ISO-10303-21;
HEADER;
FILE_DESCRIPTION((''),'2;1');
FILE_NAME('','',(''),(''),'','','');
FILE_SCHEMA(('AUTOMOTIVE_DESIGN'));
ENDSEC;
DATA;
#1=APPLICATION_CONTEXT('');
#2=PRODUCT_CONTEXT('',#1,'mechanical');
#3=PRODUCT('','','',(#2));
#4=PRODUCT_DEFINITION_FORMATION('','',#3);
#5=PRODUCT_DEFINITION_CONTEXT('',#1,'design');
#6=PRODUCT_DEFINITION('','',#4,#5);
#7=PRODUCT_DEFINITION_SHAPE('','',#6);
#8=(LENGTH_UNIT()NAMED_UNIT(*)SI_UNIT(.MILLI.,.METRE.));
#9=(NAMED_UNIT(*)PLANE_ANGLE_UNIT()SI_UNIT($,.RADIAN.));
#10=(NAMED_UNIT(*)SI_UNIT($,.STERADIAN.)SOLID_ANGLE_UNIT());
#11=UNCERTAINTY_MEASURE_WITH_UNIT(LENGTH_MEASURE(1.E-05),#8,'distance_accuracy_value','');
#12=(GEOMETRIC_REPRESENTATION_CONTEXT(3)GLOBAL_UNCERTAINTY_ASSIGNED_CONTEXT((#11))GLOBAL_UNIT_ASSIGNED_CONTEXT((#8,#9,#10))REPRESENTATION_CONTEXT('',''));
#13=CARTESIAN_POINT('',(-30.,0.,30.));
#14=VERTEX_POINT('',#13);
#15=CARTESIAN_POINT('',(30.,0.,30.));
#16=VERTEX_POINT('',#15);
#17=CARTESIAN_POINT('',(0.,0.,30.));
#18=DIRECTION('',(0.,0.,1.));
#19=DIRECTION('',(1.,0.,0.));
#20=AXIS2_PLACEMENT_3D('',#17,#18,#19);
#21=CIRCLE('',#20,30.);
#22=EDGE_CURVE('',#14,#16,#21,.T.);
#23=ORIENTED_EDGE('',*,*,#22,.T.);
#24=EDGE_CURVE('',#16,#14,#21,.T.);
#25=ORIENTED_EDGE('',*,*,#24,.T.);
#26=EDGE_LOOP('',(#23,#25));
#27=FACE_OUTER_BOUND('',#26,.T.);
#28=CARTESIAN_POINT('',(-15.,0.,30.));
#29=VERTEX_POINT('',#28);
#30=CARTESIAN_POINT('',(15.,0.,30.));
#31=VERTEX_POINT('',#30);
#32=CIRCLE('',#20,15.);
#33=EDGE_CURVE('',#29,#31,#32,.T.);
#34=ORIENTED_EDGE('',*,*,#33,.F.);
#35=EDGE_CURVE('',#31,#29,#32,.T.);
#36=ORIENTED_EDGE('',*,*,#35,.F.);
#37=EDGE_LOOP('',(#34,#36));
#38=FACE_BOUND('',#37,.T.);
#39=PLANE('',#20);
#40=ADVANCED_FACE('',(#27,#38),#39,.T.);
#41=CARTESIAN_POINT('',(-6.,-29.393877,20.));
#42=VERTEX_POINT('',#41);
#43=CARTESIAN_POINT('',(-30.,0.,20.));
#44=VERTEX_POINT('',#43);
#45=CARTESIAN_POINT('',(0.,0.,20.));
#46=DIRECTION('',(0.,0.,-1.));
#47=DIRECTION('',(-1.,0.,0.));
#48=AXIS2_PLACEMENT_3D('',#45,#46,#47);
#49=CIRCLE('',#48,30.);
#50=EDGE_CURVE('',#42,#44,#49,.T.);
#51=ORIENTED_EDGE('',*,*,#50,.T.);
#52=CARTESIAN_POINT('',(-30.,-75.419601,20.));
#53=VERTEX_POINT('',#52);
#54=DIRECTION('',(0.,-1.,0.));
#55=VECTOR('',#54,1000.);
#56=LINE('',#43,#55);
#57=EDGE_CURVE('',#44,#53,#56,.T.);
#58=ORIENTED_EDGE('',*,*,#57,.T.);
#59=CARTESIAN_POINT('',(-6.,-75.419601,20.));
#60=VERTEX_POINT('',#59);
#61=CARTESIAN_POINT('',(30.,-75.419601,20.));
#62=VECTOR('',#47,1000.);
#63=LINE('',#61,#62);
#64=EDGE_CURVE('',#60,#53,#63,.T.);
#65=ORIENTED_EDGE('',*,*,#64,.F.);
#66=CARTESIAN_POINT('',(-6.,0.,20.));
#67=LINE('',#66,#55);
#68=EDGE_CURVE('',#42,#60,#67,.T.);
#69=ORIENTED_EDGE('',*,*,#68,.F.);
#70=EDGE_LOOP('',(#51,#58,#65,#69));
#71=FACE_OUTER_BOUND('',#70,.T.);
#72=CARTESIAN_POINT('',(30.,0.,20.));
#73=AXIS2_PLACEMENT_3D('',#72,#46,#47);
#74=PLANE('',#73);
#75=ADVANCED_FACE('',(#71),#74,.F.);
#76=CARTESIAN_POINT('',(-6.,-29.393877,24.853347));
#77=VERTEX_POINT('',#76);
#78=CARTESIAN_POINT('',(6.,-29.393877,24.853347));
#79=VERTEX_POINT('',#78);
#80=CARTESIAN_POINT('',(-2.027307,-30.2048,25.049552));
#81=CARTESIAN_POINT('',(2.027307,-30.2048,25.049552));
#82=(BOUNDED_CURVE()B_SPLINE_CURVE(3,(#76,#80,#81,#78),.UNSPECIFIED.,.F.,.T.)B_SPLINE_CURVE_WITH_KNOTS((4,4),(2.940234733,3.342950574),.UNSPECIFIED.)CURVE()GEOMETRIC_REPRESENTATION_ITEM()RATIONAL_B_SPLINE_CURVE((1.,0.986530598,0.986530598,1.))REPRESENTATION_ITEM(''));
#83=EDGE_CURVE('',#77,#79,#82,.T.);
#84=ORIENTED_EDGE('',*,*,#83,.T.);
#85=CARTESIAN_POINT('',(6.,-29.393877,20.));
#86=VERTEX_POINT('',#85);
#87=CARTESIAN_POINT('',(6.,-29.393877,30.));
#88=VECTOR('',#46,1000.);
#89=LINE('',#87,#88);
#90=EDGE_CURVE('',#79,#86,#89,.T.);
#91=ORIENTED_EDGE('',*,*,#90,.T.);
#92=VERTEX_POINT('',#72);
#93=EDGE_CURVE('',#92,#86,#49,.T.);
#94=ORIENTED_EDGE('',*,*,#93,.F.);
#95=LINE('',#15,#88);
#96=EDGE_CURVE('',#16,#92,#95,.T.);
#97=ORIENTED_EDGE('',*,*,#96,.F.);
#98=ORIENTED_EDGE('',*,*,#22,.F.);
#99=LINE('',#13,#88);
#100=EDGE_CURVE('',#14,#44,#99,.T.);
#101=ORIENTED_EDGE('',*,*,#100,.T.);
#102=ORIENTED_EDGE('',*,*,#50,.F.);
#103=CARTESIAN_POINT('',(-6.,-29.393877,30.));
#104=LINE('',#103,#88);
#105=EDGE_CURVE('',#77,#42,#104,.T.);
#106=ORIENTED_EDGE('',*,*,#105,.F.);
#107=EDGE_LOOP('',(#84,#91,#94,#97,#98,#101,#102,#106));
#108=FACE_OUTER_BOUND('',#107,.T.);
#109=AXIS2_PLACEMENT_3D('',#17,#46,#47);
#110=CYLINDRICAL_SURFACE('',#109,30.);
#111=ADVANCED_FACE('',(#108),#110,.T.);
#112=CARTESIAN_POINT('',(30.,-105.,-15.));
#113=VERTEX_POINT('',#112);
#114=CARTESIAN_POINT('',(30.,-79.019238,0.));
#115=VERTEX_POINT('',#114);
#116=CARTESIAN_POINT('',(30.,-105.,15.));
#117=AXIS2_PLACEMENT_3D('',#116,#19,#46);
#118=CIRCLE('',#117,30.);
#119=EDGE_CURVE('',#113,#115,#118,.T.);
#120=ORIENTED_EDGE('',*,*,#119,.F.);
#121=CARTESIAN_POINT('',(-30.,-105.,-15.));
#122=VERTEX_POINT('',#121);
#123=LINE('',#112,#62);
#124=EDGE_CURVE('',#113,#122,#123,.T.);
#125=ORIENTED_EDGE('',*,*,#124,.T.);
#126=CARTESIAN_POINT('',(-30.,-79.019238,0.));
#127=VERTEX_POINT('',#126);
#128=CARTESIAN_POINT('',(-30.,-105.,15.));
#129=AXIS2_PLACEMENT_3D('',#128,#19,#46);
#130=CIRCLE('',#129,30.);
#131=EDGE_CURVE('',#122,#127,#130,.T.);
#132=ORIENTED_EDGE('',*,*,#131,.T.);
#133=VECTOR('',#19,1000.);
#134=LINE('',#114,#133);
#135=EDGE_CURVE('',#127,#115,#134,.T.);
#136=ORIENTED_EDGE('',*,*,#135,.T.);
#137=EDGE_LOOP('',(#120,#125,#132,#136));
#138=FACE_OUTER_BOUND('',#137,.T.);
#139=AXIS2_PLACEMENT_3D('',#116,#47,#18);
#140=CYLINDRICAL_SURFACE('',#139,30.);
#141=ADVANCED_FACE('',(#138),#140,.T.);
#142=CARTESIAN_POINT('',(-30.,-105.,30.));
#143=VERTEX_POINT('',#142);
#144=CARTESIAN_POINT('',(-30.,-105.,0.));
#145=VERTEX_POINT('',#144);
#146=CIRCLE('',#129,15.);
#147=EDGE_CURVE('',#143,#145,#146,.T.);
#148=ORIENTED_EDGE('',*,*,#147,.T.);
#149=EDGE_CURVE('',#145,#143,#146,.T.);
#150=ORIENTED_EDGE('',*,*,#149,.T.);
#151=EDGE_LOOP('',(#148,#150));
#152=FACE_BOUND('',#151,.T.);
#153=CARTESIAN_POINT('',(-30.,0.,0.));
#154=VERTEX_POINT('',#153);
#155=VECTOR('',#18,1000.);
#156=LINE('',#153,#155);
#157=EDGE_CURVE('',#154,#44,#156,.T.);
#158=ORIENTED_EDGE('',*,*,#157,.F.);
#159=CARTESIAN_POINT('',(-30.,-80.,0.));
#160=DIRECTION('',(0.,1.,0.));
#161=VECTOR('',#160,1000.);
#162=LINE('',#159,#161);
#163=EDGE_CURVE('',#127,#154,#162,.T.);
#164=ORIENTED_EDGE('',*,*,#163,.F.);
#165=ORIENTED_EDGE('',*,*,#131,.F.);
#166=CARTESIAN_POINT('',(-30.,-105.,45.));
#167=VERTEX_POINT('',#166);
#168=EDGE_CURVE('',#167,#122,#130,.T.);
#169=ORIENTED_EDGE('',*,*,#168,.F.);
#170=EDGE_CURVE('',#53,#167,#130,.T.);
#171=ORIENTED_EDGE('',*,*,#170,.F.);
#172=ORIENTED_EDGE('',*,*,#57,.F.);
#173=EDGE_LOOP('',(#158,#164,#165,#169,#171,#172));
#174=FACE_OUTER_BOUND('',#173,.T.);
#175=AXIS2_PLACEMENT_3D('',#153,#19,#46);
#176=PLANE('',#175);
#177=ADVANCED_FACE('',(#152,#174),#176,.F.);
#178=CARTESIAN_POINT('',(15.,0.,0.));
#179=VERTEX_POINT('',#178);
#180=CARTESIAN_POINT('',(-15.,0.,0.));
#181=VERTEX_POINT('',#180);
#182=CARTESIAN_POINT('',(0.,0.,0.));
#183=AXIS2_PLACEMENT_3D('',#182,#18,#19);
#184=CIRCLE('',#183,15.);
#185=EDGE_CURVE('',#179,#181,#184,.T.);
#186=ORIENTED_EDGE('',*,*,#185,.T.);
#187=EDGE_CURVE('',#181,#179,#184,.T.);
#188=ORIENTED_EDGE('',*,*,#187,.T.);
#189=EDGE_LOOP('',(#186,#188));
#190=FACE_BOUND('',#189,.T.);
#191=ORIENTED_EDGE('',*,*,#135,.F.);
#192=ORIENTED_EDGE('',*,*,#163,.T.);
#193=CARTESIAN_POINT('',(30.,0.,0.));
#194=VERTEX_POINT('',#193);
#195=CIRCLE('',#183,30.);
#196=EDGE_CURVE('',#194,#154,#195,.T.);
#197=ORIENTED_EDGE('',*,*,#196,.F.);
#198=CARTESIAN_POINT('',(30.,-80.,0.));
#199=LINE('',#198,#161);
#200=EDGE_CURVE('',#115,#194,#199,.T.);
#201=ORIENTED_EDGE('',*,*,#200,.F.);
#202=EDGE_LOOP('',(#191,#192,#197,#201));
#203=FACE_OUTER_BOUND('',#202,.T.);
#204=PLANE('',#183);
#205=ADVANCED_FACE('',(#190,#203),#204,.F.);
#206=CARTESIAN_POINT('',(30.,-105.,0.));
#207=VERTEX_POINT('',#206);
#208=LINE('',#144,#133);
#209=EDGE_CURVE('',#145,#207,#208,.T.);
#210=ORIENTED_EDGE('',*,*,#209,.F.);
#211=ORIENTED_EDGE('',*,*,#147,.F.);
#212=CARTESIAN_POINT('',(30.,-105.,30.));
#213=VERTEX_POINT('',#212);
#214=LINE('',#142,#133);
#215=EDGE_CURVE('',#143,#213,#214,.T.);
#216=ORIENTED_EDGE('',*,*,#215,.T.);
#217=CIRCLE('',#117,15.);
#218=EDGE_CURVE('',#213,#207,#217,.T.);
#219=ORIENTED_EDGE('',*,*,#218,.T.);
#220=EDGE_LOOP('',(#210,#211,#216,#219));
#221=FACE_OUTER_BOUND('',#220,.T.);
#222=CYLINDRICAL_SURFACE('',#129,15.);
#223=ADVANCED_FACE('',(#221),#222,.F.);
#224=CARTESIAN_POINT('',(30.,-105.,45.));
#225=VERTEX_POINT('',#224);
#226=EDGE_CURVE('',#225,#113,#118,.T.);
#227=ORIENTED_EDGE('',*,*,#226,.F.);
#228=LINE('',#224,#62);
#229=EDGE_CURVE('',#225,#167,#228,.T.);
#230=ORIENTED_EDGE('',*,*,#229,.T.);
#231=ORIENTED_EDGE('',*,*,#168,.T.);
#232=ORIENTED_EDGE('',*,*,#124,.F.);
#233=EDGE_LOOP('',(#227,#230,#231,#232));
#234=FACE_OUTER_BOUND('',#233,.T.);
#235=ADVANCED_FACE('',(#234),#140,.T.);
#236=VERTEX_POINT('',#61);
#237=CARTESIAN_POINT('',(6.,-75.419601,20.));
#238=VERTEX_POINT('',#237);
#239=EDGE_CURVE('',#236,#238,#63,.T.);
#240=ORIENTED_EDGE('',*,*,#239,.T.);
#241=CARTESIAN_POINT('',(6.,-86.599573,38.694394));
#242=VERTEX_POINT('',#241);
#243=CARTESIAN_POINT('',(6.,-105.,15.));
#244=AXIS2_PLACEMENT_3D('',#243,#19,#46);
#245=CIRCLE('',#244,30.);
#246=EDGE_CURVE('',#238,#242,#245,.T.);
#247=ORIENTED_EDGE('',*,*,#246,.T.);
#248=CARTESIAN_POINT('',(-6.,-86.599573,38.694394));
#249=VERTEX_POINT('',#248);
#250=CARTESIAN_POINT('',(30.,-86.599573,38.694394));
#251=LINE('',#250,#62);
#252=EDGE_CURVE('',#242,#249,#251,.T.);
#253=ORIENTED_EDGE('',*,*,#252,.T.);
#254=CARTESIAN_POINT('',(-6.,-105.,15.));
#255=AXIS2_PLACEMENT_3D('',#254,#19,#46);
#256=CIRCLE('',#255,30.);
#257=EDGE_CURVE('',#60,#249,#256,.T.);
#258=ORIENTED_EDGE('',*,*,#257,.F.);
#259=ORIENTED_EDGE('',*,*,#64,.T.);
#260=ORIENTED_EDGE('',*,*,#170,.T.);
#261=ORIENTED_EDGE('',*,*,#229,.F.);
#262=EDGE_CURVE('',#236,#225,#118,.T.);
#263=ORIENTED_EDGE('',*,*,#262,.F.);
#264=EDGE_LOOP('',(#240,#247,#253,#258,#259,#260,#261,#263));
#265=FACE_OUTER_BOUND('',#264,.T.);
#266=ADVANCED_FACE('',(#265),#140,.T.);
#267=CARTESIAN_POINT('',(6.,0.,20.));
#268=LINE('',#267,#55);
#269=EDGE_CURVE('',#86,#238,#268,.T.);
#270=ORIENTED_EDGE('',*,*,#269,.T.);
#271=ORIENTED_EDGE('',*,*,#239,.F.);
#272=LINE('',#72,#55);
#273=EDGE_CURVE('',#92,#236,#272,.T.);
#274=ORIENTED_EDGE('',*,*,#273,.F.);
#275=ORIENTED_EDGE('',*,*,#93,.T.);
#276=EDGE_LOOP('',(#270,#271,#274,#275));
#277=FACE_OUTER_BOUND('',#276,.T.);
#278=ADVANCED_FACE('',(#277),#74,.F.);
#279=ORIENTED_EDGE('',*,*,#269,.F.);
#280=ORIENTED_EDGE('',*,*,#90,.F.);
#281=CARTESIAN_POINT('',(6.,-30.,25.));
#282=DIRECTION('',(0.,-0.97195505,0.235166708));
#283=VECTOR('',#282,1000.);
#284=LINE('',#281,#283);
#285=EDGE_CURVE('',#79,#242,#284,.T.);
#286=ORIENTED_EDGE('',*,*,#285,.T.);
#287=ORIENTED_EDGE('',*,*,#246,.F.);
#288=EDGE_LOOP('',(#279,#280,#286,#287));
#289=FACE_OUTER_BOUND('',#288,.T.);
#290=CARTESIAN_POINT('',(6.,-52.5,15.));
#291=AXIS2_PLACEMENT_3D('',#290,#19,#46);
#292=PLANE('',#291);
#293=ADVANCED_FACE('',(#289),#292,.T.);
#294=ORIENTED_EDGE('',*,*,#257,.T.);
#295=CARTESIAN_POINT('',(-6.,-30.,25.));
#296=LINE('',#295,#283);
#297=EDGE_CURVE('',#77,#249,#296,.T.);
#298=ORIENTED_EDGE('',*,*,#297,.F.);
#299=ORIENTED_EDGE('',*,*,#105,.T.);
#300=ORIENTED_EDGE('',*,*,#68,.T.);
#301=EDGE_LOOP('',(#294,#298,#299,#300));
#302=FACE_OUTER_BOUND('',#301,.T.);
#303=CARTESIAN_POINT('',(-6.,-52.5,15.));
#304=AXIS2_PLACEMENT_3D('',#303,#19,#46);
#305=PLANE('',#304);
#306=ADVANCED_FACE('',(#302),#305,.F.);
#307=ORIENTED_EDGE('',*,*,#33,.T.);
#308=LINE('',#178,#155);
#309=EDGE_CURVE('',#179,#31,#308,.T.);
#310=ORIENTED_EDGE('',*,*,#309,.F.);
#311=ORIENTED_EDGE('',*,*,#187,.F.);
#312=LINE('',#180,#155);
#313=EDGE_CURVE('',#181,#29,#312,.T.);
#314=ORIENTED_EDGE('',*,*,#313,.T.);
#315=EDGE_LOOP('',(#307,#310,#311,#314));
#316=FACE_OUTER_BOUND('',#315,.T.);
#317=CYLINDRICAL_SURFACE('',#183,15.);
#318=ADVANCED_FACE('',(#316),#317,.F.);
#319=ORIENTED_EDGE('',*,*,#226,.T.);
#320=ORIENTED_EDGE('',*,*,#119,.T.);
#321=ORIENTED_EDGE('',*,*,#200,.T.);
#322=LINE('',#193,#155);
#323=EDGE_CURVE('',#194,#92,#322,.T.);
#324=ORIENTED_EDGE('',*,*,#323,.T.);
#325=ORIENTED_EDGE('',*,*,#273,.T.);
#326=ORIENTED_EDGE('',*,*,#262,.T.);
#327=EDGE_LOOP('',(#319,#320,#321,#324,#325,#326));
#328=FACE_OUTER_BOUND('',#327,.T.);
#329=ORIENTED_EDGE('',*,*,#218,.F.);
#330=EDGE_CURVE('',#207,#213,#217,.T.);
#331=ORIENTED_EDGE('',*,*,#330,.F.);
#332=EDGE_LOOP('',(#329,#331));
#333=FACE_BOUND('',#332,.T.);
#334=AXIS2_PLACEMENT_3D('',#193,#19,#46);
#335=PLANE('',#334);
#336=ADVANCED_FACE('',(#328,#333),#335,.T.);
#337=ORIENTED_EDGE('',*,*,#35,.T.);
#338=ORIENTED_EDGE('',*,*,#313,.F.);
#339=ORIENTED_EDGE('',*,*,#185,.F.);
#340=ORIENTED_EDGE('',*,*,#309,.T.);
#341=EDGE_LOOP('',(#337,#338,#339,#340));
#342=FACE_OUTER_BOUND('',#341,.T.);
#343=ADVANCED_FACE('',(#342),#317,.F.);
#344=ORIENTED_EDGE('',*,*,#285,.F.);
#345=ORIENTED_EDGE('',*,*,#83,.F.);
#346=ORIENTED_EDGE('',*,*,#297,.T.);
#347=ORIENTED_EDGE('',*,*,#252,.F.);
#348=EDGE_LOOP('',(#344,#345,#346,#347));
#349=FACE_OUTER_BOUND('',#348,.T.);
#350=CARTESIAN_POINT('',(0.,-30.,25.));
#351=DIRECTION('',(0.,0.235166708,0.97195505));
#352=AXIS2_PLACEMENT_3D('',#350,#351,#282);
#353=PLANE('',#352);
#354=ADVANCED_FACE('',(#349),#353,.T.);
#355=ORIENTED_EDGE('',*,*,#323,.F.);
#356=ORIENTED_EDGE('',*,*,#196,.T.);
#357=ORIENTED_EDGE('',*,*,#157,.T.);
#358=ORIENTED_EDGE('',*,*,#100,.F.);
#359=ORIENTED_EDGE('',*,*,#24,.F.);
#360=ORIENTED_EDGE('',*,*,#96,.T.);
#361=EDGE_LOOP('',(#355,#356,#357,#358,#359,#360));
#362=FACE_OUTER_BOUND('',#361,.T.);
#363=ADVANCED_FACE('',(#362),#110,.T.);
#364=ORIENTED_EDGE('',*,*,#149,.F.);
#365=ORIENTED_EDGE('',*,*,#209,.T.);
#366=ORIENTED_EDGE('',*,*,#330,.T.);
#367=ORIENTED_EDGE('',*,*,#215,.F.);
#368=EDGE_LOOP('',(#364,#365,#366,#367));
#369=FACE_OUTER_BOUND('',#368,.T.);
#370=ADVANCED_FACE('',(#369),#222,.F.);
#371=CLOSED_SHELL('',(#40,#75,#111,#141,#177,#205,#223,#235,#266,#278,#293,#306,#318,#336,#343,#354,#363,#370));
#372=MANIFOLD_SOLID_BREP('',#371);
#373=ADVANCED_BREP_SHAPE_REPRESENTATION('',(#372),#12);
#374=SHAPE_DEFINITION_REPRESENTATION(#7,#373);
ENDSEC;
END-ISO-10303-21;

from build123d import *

# Parameters (mm, degrees)
UPPER_EYE_SKETCH_R      = 30
UPPER_EYE_BOSS_DEPTH    = 30
UPPER_EYE_BORE_SKETCH_R = 15
UPPER_EYE_BORE_DEPTH    = 52.961524227
ARM_PROFILE_SKETCH_W    = 20
ARM_PROFILE_SKETCH_H    = 80
ARM_DEPTH               = 30
ARM_START               = 60
ARM_TRIM_CUT_DEPTH      = 60
LOWER_EYE_SKETCH_R      = 30
LOWER_EYE_BOSS_DEPTH    = 30
ARM_RIB_12MM_REACH      = 147.43
ARM_RIB_SKETCH_WALL_W   = 351.093498284
ARM_RIB_SKETCH_WALL_H   = 12
LOWER_EYE_BORE_SKETCH_R = 15
LOWER_EYE_BORE_DEPTH    = 155.434452115


with BuildPart() as part:
    # Upper Eye Sketch → Upper Eye Boss (new body)
    with BuildSketch(Plane.XY):
        Circle(UPPER_EYE_SKETCH_R)
    extrude(amount=UPPER_EYE_BOSS_DEPTH)

    # Upper Eye Bore Sketch → Upper Eye Bore (cut, through all)
    with BuildSketch(Plane.XY.offset(30)):
        Circle(UPPER_EYE_BORE_SKETCH_R)
    extrude(amount=-UPPER_EYE_BORE_DEPTH, mode=Mode.SUBTRACT)

    # Arm Profile Sketch → Arm (add, symmetric)
    with BuildSketch(Plane(origin=(0, 0, 0), x_dir=(0, 0, -1), z_dir=(1, 0, 0))):
        with Locations((-10, -40)):
            Rectangle(ARM_PROFILE_SKETCH_W, ARM_PROFILE_SKETCH_H)
    extrude(amount=ARM_DEPTH, both=True)

    # Arm Trim Sketch → Arm Trim Cut (cut)
    with BuildSketch(Plane.XY.offset(ARM_START)):
        with BuildLine():
            Line((15, 0), (-15, 0))
            ThreePointArc((-15, 0), (0, -15), (15, 0))
        make_face()
    extrude(amount=-ARM_TRIM_CUT_DEPTH, mode=Mode.SUBTRACT)

    # Lower Eye Sketch → Lower Eye Boss (add, symmetric)
    with BuildSketch(Plane(origin=(0, 0, 0), x_dir=(0, 0, -1), z_dir=(1, 0, 0))):
        with Locations((-15, -105)):
            Circle(LOWER_EYE_SKETCH_R)
    extrude(amount=LOWER_EYE_BOSS_DEPTH, both=True)

    # Arm Rib Sketch wall → Arm Rib 12mm (add, up to next)
    with BuildSketch(Plane(origin=(0, -58.299786749, 31.847196974), x_dir=(0, -0.971955050189, 0.235166707705), z_dir=(0, -0.235166707705, -0.971955050189)), mode=Mode.PRIVATE) as arm_rib_12mm_sk1:
        Rectangle(ARM_RIB_SKETCH_WALL_W, ARM_RIB_SKETCH_WALL_H)
    arm_rib_12mm_tool1 = extrude(arm_rib_12mm_sk1.sketch, amount=ARM_RIB_12MM_REACH, mode=Mode.PRIVATE) - part.part
    add(arm_rib_12mm_tool1.solids().sort_by_distance((0, -58.299786749, 31.847196974))[0])

    # Lower Eye Bore Sketch → Lower Eye Bore (cut, through all)
    with BuildSketch(Plane(origin=(30, 0, 0), x_dir=(0, 0, -1), z_dir=(1, 0, 0))):
        with Locations((-15, -105)):
            Circle(LOWER_EYE_BORE_SKETCH_R)
    extrude(amount=-LOWER_EYE_BORE_DEPTH, mode=Mode.SUBTRACT)


solid = part.part
